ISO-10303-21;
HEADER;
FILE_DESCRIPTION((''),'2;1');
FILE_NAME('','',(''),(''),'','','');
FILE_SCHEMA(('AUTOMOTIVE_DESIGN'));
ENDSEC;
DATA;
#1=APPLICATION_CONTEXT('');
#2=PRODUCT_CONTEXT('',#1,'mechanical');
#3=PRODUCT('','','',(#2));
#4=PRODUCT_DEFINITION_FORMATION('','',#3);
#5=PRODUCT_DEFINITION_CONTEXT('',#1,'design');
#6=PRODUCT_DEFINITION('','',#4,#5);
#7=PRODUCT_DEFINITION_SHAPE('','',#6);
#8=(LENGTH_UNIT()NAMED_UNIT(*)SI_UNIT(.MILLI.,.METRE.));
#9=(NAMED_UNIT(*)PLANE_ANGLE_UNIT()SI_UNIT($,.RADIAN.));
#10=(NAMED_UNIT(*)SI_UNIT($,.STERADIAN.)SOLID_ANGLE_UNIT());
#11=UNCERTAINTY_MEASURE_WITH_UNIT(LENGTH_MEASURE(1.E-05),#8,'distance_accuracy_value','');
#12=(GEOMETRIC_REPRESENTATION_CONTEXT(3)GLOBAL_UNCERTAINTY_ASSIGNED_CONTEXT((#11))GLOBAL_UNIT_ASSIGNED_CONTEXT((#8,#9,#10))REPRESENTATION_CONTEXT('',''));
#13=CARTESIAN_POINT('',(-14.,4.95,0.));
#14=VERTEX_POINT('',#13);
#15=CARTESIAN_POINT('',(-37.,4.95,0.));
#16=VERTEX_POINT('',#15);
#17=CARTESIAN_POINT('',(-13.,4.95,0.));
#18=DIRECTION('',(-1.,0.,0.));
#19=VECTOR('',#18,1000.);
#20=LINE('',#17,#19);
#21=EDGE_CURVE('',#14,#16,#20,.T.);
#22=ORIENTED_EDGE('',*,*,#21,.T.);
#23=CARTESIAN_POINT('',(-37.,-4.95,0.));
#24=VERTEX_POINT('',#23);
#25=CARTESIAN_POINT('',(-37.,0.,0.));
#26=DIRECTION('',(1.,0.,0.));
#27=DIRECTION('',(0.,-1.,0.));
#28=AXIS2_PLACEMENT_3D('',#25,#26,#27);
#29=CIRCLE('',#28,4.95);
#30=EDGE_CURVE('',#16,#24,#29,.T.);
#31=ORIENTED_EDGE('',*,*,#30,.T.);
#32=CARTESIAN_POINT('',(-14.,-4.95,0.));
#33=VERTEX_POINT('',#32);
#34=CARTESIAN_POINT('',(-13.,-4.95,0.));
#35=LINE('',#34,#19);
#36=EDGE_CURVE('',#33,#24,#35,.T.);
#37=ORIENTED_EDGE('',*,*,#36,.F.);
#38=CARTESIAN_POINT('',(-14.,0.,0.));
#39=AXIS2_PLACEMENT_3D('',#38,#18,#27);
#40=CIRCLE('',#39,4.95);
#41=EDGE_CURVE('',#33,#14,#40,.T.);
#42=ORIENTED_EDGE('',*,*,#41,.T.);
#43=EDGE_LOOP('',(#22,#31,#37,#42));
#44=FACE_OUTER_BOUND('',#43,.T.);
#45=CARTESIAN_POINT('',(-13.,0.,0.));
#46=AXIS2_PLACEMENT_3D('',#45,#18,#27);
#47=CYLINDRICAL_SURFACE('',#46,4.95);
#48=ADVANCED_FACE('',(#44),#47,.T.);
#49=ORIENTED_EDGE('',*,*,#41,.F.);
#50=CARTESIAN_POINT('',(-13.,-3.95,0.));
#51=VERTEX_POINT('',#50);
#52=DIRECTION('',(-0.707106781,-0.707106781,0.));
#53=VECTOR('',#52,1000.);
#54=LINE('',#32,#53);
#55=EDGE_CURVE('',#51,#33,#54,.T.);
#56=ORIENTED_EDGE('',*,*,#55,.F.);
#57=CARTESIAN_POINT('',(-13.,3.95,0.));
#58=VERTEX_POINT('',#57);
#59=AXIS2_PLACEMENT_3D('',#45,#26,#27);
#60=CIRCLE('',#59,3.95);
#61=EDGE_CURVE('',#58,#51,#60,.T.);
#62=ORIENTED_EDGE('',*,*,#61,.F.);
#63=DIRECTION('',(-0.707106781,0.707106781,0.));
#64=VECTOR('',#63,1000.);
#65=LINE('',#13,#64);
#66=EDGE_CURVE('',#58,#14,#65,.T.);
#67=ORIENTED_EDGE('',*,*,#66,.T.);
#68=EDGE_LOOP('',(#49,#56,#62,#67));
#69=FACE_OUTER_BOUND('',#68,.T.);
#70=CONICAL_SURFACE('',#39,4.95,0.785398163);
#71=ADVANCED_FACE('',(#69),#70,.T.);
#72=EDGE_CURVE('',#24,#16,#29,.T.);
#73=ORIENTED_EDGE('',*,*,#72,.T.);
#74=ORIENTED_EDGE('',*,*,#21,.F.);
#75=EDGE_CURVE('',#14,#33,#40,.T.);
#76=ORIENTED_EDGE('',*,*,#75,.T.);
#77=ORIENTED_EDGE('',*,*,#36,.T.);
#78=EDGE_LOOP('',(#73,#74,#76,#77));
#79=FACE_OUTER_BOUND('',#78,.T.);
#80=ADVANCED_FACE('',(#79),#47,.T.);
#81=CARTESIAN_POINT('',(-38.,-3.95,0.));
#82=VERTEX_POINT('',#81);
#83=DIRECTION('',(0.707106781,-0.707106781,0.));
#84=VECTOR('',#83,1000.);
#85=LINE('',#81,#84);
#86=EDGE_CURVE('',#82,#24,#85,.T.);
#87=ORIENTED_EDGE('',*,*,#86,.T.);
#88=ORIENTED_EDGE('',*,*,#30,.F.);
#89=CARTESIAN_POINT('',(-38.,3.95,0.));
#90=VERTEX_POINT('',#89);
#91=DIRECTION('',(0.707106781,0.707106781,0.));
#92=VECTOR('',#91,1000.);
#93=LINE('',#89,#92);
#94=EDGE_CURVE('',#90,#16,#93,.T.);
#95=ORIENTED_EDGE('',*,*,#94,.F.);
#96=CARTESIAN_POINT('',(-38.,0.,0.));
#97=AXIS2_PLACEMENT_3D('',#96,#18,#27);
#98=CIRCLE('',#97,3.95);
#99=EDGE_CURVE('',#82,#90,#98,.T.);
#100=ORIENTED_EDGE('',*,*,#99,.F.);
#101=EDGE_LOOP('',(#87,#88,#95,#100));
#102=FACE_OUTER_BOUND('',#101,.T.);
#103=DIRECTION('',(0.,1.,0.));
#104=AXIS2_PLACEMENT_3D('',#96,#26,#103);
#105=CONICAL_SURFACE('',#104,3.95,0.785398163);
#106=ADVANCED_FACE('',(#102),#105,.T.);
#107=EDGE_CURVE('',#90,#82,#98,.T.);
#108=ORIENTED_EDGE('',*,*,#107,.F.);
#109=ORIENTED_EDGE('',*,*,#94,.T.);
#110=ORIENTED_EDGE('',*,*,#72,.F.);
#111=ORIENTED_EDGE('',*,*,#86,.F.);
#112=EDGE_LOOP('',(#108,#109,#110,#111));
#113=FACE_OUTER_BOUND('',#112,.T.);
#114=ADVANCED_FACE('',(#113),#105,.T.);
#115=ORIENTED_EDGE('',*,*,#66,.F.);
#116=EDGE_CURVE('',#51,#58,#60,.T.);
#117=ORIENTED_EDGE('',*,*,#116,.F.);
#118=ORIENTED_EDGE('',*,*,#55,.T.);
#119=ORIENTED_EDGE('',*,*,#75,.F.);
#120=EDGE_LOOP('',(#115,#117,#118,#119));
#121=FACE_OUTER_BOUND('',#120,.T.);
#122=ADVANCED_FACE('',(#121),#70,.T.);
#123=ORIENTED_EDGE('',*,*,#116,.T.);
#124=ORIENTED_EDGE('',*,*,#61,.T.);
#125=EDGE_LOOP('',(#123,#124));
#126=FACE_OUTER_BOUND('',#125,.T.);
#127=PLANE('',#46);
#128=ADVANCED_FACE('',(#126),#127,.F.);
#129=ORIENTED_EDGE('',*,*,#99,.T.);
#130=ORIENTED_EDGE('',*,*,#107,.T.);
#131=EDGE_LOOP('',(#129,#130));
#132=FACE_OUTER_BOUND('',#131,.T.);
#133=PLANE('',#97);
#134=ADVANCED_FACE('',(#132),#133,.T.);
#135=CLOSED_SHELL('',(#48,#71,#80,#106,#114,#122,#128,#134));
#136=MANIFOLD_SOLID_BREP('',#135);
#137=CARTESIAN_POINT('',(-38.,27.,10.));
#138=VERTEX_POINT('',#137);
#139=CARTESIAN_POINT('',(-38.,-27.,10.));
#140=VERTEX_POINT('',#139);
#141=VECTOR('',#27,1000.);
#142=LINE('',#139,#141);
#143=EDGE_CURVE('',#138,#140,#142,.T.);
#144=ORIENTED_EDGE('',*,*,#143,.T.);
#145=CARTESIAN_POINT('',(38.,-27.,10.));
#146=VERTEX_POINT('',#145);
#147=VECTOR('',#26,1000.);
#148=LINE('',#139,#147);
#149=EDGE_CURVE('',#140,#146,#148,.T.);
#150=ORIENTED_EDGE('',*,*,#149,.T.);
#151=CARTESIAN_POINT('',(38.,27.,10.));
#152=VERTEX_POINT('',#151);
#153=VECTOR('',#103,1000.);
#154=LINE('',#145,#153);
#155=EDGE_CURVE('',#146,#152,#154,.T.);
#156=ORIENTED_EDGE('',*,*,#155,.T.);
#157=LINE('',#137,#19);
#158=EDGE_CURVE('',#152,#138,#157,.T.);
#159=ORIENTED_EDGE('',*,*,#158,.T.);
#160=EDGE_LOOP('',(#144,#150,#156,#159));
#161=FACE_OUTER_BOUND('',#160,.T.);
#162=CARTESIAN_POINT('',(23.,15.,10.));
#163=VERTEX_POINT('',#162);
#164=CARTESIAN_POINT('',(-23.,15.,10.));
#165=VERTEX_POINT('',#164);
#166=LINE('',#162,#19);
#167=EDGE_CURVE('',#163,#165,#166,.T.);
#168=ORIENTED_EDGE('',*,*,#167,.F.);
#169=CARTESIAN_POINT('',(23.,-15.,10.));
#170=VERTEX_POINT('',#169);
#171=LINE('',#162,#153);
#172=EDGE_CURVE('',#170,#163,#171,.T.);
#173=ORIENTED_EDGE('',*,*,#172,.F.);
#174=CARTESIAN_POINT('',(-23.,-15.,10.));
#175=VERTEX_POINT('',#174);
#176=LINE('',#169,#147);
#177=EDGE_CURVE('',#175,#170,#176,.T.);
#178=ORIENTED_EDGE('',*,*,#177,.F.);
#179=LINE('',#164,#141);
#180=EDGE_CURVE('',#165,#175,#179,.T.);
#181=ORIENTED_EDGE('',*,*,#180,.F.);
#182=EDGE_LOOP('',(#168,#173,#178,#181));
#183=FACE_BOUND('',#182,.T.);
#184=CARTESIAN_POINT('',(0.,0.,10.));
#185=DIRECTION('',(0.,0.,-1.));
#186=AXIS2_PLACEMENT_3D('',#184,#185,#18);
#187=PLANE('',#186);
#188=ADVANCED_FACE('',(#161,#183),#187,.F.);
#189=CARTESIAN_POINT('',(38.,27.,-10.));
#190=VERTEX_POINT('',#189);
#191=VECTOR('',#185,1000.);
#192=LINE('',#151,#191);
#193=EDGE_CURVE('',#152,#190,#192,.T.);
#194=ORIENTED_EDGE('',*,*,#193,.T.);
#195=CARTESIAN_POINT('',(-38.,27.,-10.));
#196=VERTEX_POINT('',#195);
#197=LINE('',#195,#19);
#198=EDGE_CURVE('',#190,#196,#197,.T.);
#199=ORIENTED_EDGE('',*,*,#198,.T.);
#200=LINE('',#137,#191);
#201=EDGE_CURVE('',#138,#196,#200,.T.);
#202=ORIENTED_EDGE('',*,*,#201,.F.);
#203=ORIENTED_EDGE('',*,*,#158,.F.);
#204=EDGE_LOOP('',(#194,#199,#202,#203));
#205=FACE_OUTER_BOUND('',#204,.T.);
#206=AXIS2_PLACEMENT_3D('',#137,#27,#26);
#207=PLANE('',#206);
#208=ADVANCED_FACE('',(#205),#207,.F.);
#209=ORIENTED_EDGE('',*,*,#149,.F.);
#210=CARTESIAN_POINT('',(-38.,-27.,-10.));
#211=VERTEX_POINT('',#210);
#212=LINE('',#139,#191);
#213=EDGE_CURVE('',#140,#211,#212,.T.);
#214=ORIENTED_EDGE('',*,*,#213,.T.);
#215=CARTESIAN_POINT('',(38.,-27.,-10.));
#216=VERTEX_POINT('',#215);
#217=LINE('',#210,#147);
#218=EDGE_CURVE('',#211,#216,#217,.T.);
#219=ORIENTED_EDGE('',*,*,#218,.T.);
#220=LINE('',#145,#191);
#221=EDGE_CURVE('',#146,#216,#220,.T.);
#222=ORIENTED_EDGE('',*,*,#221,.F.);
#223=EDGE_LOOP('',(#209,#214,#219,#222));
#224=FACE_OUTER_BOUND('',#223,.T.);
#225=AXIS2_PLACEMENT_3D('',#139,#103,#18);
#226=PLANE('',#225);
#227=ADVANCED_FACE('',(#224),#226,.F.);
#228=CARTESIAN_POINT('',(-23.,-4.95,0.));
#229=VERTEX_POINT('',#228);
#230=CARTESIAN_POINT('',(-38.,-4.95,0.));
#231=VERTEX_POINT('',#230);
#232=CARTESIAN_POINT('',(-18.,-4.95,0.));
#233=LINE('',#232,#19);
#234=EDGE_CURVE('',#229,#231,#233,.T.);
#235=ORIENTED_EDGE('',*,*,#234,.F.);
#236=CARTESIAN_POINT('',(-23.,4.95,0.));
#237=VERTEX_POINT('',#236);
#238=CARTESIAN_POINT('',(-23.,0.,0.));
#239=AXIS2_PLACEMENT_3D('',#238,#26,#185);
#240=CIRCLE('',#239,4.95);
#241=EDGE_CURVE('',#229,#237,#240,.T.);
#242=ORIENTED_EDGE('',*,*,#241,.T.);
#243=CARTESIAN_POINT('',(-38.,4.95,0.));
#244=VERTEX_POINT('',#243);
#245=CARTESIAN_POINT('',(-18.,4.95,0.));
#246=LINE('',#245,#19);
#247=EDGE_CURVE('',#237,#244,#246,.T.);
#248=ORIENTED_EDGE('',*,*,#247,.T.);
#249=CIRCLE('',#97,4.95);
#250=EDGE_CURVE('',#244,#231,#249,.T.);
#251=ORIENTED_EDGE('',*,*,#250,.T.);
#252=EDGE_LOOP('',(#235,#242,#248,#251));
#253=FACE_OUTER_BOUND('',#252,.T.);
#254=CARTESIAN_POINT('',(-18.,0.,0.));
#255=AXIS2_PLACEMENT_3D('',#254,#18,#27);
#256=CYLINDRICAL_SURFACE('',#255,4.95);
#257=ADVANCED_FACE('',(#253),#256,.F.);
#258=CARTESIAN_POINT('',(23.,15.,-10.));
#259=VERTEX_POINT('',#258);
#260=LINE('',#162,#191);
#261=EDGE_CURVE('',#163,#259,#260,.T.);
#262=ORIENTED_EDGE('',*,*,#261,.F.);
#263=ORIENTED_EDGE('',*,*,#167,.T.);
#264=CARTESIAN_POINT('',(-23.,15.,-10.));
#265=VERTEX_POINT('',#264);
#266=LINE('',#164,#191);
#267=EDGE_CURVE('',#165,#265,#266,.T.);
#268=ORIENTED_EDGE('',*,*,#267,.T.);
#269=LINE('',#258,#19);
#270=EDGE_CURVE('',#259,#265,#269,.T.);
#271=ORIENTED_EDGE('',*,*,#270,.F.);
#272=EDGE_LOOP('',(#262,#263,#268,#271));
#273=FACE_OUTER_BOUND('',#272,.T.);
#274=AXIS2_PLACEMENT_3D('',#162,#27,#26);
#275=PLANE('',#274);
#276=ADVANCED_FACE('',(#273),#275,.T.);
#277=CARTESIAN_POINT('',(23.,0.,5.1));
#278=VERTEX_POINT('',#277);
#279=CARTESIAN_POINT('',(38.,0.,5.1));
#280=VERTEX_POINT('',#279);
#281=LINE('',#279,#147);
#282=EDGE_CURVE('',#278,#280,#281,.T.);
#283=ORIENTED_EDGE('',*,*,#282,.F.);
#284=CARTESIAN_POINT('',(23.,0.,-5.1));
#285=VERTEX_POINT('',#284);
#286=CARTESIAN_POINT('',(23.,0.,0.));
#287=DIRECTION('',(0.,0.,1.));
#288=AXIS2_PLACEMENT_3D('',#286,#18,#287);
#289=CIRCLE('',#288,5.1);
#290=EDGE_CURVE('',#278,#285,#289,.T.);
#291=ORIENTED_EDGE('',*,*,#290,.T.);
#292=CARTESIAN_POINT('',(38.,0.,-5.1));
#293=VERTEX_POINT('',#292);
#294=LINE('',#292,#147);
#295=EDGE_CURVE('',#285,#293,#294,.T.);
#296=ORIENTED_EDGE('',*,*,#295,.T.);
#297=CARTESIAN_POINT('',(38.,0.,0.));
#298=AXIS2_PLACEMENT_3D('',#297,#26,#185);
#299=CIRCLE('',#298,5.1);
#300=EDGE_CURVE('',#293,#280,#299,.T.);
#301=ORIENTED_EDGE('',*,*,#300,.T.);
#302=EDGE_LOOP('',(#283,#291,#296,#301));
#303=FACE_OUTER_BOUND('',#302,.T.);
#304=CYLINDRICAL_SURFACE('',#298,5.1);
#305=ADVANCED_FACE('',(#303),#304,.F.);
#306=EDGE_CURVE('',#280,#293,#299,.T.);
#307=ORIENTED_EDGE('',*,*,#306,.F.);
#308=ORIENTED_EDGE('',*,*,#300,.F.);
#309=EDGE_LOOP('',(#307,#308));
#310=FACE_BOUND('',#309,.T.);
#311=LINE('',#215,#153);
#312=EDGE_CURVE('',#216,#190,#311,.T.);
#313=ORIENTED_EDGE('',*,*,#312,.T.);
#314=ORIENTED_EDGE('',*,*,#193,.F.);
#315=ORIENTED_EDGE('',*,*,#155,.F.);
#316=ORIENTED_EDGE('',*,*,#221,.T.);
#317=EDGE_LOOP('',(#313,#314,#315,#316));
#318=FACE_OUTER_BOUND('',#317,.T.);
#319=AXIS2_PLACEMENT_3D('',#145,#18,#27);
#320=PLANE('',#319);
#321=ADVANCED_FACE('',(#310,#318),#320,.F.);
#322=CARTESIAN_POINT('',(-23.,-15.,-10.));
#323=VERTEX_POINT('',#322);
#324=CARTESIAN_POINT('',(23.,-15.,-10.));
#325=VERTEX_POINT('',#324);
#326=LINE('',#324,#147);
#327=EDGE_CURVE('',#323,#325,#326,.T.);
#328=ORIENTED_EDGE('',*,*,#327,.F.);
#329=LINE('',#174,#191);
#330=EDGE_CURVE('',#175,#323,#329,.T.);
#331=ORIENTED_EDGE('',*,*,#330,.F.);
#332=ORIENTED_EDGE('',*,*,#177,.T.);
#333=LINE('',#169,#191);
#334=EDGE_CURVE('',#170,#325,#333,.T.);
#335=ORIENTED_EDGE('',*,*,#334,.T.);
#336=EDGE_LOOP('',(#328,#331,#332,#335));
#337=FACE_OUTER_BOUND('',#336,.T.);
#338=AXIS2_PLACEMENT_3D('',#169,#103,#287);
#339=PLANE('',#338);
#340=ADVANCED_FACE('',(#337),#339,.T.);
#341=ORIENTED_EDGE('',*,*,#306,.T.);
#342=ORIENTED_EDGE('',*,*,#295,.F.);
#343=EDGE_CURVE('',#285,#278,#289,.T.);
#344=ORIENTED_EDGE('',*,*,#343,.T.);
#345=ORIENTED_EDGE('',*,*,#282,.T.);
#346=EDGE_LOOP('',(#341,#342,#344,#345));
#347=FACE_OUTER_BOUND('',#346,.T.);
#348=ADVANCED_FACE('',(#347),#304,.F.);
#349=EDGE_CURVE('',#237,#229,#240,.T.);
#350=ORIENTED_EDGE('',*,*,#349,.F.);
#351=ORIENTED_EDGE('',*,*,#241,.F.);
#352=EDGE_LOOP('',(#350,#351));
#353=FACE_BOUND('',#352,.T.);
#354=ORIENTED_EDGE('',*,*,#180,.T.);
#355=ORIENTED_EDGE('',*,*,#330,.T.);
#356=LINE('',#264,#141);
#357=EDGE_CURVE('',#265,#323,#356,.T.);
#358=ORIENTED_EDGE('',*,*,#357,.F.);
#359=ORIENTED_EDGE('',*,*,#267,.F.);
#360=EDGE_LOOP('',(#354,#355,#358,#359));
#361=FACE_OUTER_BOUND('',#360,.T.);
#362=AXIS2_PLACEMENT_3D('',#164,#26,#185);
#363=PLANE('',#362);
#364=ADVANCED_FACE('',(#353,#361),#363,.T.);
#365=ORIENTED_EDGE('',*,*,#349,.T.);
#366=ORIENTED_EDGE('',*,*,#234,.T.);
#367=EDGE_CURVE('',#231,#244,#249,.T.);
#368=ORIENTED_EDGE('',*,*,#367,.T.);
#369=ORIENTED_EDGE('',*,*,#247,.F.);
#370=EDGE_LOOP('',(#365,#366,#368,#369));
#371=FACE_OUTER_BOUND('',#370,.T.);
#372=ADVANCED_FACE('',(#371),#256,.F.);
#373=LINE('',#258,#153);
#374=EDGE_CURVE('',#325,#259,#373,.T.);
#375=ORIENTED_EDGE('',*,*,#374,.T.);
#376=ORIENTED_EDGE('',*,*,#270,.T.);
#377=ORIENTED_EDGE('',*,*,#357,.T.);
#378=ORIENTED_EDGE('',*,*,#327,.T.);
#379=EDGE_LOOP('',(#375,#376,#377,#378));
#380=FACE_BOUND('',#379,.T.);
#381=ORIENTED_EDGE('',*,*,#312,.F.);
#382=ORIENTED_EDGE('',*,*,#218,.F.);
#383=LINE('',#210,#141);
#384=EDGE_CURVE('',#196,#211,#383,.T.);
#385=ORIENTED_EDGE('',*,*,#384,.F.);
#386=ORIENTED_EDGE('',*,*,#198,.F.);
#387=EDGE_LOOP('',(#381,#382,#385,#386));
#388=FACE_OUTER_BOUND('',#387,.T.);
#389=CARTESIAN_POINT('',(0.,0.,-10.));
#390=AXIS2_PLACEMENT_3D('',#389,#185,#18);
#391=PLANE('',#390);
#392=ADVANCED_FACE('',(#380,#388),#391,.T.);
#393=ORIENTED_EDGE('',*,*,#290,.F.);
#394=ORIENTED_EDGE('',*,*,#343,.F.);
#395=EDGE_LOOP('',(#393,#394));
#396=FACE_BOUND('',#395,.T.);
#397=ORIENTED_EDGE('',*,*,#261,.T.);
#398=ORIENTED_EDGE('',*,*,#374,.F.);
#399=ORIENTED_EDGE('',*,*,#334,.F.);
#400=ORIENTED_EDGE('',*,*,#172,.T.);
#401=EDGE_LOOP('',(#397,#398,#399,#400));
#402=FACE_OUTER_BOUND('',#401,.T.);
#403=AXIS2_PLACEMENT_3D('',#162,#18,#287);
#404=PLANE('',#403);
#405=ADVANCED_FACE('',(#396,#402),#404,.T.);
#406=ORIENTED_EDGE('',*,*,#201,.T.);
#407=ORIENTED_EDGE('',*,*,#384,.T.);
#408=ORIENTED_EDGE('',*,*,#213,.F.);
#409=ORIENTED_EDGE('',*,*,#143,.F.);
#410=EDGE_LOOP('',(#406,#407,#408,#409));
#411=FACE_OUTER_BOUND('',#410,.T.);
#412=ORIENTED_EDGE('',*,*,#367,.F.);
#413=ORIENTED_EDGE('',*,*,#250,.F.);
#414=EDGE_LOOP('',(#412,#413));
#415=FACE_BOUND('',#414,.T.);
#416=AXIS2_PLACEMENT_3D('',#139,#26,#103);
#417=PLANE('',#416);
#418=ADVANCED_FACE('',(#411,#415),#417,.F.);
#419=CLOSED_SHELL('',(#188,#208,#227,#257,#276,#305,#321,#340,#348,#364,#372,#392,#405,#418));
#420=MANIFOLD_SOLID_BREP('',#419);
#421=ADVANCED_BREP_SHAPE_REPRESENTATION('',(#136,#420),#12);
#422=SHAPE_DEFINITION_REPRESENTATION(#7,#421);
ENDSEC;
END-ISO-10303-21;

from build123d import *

# Parameters (mm, degrees)
SKETCH_1_W              = 76
SKETCH_1_H              = 54
SKETCH_1_W_2            = 46
SKETCH_1_H_2            = 30
EXTRUDE_1_DEPTH         = 10
SKETCH_2_R              = 4.95
CUT_EXTRUDE_1_DEPTH     = 20
HOLE_WIZARD_M12_1_D     = 10.2
HOLE_WIZARD_M12_1_DEPTH = 32.75
HOLE_WIZARD_M12_1_TIP   = 3.064389157
SKETCH_5_R              = 4.95
EXTRUDE_2_DEPTH         = 25
CHAMFER_1_SIZE          = 1


with BuildPart() as part:
    # 草图1 → 凸台-拉伸1 (new, symmetric)
    with BuildSketch(Plane.XY):
        Rectangle(SKETCH_1_W, SKETCH_1_H)
        Rectangle(SKETCH_1_W_2, SKETCH_1_H_2, mode=Mode.SUBTRACT)
    extrude(amount=EXTRUDE_1_DEPTH, both=True)

    # 草图2 → 切除-拉伸1 (cut)
    with BuildSketch(Plane.ZY.offset(38)):
        with Locations(Location((0, 0, 0), (0, 0, 270))):
            Circle(SKETCH_2_R)
    extrude(amount=-CUT_EXTRUDE_1_DEPTH, mode=Mode.SUBTRACT)

    # M12 螺纹孔1
    with Locations(Plane(origin=(38, 0, 0), x_dir=(0, 0, -1), z_dir=(1, 0, 0))):
        with Locations((0, 0)):
            Hole(HOLE_WIZARD_M12_1_D / 2, depth=HOLE_WIZARD_M12_1_DEPTH)
            with Locations((0, 0, -(HOLE_WIZARD_M12_1_DEPTH + HOLE_WIZARD_M12_1_TIP / 2))):  # 118° drill point
                Cone(0, HOLE_WIZARD_M12_1_D / 2, HOLE_WIZARD_M12_1_TIP, mode=Mode.SUBTRACT)


with BuildPart() as body_2:
    # 草图5 → 凸台-拉伸2 (new body)
    with BuildSketch(Plane.ZY.offset(38)):
        with Locations(Location((0, 0, 0), (0, 0, 270))):
            Circle(SKETCH_5_R)
    extrude(amount=-EXTRUDE_2_DEPTH)

    # 倒角1
    chamfer_1_edges = [body_2.edges().sort_by_distance(p)[0] for p in [
        (-38, 4.95, 0),
        (-13, 4.95, 0),
    ]]
    chamfer(chamfer_1_edges, length=CHAMFER_1_SIZE)


solid = Compound([part.part, body_2.part])
